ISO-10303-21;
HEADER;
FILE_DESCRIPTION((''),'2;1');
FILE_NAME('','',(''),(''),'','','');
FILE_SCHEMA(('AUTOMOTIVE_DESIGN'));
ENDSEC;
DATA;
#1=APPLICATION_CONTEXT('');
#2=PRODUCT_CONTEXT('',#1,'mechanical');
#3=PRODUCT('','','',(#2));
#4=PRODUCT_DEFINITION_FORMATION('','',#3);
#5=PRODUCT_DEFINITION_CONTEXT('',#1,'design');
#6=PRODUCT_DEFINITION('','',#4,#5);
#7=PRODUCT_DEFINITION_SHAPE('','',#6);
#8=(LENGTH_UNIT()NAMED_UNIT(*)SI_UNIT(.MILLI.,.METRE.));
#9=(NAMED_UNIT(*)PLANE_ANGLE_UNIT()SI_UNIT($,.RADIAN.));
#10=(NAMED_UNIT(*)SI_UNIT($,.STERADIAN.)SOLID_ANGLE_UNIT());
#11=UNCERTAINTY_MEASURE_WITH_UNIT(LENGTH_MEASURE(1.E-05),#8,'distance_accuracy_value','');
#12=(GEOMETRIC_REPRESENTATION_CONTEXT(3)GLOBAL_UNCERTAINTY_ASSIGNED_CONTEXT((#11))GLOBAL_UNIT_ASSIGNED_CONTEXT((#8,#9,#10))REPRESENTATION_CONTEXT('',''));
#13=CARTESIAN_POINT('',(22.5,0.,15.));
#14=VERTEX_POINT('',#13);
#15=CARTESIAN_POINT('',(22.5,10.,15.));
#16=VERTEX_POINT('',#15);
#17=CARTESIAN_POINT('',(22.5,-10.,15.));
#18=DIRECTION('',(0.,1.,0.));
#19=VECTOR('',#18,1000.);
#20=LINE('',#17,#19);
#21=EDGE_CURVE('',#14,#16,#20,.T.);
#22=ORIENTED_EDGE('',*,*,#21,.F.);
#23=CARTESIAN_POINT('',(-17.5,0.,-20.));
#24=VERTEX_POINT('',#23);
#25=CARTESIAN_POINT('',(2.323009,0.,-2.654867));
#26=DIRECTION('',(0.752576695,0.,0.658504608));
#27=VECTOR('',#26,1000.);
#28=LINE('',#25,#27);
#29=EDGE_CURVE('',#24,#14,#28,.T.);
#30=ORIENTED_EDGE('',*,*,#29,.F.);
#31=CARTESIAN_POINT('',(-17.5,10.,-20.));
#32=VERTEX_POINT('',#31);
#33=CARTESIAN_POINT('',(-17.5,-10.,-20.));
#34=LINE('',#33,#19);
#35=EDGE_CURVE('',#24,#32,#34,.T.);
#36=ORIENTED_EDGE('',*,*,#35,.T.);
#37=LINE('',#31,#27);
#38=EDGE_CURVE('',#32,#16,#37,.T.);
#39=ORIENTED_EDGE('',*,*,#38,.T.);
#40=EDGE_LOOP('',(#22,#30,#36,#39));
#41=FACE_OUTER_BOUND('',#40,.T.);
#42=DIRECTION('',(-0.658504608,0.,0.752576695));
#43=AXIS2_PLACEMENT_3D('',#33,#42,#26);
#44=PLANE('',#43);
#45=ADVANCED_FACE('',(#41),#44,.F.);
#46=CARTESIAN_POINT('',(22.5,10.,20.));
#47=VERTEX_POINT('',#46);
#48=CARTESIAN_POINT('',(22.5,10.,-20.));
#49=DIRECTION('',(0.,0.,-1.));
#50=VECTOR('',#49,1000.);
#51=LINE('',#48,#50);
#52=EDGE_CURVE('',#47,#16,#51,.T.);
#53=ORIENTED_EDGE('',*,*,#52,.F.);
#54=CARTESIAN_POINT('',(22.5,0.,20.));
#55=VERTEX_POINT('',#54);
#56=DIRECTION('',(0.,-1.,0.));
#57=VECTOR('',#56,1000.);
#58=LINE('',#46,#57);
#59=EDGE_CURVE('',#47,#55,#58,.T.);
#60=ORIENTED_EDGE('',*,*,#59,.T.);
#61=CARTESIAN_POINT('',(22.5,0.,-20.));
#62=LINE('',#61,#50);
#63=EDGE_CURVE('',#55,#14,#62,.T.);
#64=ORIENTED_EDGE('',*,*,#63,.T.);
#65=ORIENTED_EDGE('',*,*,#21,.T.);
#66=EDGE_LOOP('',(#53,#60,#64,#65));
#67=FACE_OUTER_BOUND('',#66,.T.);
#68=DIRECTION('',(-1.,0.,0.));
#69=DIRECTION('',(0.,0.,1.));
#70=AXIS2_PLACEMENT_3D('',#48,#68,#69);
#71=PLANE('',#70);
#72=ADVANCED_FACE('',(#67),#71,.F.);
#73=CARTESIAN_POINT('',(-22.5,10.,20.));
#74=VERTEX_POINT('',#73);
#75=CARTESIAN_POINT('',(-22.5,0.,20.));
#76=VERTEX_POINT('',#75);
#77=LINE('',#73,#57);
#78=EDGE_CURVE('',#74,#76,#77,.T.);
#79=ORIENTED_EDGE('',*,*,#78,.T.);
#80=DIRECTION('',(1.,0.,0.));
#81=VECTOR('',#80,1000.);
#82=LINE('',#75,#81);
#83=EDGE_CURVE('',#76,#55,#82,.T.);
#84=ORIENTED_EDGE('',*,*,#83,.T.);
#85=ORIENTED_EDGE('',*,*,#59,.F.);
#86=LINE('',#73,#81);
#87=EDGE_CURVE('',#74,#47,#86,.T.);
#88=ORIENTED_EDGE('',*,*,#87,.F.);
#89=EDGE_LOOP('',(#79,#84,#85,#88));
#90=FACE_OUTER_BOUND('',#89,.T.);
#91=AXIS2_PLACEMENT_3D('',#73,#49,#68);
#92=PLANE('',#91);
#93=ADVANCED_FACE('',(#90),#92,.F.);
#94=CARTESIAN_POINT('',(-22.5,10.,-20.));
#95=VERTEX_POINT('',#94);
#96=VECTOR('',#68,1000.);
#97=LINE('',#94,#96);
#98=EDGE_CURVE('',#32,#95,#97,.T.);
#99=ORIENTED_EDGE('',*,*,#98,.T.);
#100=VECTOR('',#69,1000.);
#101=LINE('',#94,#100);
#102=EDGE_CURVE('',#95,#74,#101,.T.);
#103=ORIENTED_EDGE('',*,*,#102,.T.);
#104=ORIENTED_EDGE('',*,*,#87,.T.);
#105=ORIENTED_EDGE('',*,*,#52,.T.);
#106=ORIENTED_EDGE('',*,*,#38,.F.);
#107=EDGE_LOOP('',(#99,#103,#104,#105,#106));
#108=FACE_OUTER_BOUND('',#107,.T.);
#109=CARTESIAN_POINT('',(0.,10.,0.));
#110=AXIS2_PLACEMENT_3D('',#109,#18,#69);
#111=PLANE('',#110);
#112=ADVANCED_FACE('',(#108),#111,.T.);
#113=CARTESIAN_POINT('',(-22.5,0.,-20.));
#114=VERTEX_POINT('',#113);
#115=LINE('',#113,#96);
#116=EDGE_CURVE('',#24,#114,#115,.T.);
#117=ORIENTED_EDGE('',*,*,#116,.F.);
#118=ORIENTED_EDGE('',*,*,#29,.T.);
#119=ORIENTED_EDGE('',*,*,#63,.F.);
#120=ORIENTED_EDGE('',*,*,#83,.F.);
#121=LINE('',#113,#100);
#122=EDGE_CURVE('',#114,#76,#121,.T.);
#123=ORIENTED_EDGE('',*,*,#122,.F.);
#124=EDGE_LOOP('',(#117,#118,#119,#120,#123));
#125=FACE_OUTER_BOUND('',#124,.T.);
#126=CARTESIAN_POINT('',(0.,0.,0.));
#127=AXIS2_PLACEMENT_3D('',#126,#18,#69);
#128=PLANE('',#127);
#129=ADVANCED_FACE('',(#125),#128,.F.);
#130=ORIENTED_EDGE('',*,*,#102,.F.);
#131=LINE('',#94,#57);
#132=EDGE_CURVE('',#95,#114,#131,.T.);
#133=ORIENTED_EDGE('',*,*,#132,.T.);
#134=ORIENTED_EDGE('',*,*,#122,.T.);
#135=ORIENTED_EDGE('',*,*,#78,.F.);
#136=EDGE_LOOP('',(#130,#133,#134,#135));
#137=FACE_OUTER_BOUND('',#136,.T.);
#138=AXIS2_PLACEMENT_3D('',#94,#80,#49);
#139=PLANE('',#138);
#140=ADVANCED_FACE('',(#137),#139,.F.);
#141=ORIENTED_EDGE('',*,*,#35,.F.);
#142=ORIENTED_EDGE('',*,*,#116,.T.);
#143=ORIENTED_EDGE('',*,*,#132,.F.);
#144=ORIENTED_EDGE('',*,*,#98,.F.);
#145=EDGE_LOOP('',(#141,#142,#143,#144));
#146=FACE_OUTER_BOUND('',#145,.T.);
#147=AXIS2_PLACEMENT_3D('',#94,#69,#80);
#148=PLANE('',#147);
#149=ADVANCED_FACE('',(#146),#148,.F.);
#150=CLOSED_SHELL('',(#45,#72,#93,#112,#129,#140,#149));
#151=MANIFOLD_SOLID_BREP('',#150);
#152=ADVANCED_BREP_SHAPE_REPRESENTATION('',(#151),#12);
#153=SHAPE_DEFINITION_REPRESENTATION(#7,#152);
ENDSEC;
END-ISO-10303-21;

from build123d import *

# Parameters (mm, degrees)
SKETCH_1_W          = 45
SKETCH_1_H          = 40
EXTRUDE_1_DEPTH     = 10
CUT_EXTRUDE_1_DEPTH = 20


with BuildPart() as part:
    # 草图1 → 凸台-拉伸1 (new body)
    with BuildSketch(Plane(origin=(0, 0, 0), x_dir=(1, 0, 0), z_dir=(0, 1, 0))):
        Rectangle(SKETCH_1_W, SKETCH_1_H)
    extrude(amount=EXTRUDE_1_DEPTH)

    # 草图2 → 切除-拉伸1 (cut)
    with BuildSketch(Plane(origin=(0, 10, 0), x_dir=(1, 0, 0), z_dir=(0, 1, 0))):
        Polygon((22.5, 20), (-17.5, 20), (22.5, -15), align=None)
    extrude(amount=-CUT_EXTRUDE_1_DEPTH, mode=Mode.SUBTRACT)


solid = part.part
